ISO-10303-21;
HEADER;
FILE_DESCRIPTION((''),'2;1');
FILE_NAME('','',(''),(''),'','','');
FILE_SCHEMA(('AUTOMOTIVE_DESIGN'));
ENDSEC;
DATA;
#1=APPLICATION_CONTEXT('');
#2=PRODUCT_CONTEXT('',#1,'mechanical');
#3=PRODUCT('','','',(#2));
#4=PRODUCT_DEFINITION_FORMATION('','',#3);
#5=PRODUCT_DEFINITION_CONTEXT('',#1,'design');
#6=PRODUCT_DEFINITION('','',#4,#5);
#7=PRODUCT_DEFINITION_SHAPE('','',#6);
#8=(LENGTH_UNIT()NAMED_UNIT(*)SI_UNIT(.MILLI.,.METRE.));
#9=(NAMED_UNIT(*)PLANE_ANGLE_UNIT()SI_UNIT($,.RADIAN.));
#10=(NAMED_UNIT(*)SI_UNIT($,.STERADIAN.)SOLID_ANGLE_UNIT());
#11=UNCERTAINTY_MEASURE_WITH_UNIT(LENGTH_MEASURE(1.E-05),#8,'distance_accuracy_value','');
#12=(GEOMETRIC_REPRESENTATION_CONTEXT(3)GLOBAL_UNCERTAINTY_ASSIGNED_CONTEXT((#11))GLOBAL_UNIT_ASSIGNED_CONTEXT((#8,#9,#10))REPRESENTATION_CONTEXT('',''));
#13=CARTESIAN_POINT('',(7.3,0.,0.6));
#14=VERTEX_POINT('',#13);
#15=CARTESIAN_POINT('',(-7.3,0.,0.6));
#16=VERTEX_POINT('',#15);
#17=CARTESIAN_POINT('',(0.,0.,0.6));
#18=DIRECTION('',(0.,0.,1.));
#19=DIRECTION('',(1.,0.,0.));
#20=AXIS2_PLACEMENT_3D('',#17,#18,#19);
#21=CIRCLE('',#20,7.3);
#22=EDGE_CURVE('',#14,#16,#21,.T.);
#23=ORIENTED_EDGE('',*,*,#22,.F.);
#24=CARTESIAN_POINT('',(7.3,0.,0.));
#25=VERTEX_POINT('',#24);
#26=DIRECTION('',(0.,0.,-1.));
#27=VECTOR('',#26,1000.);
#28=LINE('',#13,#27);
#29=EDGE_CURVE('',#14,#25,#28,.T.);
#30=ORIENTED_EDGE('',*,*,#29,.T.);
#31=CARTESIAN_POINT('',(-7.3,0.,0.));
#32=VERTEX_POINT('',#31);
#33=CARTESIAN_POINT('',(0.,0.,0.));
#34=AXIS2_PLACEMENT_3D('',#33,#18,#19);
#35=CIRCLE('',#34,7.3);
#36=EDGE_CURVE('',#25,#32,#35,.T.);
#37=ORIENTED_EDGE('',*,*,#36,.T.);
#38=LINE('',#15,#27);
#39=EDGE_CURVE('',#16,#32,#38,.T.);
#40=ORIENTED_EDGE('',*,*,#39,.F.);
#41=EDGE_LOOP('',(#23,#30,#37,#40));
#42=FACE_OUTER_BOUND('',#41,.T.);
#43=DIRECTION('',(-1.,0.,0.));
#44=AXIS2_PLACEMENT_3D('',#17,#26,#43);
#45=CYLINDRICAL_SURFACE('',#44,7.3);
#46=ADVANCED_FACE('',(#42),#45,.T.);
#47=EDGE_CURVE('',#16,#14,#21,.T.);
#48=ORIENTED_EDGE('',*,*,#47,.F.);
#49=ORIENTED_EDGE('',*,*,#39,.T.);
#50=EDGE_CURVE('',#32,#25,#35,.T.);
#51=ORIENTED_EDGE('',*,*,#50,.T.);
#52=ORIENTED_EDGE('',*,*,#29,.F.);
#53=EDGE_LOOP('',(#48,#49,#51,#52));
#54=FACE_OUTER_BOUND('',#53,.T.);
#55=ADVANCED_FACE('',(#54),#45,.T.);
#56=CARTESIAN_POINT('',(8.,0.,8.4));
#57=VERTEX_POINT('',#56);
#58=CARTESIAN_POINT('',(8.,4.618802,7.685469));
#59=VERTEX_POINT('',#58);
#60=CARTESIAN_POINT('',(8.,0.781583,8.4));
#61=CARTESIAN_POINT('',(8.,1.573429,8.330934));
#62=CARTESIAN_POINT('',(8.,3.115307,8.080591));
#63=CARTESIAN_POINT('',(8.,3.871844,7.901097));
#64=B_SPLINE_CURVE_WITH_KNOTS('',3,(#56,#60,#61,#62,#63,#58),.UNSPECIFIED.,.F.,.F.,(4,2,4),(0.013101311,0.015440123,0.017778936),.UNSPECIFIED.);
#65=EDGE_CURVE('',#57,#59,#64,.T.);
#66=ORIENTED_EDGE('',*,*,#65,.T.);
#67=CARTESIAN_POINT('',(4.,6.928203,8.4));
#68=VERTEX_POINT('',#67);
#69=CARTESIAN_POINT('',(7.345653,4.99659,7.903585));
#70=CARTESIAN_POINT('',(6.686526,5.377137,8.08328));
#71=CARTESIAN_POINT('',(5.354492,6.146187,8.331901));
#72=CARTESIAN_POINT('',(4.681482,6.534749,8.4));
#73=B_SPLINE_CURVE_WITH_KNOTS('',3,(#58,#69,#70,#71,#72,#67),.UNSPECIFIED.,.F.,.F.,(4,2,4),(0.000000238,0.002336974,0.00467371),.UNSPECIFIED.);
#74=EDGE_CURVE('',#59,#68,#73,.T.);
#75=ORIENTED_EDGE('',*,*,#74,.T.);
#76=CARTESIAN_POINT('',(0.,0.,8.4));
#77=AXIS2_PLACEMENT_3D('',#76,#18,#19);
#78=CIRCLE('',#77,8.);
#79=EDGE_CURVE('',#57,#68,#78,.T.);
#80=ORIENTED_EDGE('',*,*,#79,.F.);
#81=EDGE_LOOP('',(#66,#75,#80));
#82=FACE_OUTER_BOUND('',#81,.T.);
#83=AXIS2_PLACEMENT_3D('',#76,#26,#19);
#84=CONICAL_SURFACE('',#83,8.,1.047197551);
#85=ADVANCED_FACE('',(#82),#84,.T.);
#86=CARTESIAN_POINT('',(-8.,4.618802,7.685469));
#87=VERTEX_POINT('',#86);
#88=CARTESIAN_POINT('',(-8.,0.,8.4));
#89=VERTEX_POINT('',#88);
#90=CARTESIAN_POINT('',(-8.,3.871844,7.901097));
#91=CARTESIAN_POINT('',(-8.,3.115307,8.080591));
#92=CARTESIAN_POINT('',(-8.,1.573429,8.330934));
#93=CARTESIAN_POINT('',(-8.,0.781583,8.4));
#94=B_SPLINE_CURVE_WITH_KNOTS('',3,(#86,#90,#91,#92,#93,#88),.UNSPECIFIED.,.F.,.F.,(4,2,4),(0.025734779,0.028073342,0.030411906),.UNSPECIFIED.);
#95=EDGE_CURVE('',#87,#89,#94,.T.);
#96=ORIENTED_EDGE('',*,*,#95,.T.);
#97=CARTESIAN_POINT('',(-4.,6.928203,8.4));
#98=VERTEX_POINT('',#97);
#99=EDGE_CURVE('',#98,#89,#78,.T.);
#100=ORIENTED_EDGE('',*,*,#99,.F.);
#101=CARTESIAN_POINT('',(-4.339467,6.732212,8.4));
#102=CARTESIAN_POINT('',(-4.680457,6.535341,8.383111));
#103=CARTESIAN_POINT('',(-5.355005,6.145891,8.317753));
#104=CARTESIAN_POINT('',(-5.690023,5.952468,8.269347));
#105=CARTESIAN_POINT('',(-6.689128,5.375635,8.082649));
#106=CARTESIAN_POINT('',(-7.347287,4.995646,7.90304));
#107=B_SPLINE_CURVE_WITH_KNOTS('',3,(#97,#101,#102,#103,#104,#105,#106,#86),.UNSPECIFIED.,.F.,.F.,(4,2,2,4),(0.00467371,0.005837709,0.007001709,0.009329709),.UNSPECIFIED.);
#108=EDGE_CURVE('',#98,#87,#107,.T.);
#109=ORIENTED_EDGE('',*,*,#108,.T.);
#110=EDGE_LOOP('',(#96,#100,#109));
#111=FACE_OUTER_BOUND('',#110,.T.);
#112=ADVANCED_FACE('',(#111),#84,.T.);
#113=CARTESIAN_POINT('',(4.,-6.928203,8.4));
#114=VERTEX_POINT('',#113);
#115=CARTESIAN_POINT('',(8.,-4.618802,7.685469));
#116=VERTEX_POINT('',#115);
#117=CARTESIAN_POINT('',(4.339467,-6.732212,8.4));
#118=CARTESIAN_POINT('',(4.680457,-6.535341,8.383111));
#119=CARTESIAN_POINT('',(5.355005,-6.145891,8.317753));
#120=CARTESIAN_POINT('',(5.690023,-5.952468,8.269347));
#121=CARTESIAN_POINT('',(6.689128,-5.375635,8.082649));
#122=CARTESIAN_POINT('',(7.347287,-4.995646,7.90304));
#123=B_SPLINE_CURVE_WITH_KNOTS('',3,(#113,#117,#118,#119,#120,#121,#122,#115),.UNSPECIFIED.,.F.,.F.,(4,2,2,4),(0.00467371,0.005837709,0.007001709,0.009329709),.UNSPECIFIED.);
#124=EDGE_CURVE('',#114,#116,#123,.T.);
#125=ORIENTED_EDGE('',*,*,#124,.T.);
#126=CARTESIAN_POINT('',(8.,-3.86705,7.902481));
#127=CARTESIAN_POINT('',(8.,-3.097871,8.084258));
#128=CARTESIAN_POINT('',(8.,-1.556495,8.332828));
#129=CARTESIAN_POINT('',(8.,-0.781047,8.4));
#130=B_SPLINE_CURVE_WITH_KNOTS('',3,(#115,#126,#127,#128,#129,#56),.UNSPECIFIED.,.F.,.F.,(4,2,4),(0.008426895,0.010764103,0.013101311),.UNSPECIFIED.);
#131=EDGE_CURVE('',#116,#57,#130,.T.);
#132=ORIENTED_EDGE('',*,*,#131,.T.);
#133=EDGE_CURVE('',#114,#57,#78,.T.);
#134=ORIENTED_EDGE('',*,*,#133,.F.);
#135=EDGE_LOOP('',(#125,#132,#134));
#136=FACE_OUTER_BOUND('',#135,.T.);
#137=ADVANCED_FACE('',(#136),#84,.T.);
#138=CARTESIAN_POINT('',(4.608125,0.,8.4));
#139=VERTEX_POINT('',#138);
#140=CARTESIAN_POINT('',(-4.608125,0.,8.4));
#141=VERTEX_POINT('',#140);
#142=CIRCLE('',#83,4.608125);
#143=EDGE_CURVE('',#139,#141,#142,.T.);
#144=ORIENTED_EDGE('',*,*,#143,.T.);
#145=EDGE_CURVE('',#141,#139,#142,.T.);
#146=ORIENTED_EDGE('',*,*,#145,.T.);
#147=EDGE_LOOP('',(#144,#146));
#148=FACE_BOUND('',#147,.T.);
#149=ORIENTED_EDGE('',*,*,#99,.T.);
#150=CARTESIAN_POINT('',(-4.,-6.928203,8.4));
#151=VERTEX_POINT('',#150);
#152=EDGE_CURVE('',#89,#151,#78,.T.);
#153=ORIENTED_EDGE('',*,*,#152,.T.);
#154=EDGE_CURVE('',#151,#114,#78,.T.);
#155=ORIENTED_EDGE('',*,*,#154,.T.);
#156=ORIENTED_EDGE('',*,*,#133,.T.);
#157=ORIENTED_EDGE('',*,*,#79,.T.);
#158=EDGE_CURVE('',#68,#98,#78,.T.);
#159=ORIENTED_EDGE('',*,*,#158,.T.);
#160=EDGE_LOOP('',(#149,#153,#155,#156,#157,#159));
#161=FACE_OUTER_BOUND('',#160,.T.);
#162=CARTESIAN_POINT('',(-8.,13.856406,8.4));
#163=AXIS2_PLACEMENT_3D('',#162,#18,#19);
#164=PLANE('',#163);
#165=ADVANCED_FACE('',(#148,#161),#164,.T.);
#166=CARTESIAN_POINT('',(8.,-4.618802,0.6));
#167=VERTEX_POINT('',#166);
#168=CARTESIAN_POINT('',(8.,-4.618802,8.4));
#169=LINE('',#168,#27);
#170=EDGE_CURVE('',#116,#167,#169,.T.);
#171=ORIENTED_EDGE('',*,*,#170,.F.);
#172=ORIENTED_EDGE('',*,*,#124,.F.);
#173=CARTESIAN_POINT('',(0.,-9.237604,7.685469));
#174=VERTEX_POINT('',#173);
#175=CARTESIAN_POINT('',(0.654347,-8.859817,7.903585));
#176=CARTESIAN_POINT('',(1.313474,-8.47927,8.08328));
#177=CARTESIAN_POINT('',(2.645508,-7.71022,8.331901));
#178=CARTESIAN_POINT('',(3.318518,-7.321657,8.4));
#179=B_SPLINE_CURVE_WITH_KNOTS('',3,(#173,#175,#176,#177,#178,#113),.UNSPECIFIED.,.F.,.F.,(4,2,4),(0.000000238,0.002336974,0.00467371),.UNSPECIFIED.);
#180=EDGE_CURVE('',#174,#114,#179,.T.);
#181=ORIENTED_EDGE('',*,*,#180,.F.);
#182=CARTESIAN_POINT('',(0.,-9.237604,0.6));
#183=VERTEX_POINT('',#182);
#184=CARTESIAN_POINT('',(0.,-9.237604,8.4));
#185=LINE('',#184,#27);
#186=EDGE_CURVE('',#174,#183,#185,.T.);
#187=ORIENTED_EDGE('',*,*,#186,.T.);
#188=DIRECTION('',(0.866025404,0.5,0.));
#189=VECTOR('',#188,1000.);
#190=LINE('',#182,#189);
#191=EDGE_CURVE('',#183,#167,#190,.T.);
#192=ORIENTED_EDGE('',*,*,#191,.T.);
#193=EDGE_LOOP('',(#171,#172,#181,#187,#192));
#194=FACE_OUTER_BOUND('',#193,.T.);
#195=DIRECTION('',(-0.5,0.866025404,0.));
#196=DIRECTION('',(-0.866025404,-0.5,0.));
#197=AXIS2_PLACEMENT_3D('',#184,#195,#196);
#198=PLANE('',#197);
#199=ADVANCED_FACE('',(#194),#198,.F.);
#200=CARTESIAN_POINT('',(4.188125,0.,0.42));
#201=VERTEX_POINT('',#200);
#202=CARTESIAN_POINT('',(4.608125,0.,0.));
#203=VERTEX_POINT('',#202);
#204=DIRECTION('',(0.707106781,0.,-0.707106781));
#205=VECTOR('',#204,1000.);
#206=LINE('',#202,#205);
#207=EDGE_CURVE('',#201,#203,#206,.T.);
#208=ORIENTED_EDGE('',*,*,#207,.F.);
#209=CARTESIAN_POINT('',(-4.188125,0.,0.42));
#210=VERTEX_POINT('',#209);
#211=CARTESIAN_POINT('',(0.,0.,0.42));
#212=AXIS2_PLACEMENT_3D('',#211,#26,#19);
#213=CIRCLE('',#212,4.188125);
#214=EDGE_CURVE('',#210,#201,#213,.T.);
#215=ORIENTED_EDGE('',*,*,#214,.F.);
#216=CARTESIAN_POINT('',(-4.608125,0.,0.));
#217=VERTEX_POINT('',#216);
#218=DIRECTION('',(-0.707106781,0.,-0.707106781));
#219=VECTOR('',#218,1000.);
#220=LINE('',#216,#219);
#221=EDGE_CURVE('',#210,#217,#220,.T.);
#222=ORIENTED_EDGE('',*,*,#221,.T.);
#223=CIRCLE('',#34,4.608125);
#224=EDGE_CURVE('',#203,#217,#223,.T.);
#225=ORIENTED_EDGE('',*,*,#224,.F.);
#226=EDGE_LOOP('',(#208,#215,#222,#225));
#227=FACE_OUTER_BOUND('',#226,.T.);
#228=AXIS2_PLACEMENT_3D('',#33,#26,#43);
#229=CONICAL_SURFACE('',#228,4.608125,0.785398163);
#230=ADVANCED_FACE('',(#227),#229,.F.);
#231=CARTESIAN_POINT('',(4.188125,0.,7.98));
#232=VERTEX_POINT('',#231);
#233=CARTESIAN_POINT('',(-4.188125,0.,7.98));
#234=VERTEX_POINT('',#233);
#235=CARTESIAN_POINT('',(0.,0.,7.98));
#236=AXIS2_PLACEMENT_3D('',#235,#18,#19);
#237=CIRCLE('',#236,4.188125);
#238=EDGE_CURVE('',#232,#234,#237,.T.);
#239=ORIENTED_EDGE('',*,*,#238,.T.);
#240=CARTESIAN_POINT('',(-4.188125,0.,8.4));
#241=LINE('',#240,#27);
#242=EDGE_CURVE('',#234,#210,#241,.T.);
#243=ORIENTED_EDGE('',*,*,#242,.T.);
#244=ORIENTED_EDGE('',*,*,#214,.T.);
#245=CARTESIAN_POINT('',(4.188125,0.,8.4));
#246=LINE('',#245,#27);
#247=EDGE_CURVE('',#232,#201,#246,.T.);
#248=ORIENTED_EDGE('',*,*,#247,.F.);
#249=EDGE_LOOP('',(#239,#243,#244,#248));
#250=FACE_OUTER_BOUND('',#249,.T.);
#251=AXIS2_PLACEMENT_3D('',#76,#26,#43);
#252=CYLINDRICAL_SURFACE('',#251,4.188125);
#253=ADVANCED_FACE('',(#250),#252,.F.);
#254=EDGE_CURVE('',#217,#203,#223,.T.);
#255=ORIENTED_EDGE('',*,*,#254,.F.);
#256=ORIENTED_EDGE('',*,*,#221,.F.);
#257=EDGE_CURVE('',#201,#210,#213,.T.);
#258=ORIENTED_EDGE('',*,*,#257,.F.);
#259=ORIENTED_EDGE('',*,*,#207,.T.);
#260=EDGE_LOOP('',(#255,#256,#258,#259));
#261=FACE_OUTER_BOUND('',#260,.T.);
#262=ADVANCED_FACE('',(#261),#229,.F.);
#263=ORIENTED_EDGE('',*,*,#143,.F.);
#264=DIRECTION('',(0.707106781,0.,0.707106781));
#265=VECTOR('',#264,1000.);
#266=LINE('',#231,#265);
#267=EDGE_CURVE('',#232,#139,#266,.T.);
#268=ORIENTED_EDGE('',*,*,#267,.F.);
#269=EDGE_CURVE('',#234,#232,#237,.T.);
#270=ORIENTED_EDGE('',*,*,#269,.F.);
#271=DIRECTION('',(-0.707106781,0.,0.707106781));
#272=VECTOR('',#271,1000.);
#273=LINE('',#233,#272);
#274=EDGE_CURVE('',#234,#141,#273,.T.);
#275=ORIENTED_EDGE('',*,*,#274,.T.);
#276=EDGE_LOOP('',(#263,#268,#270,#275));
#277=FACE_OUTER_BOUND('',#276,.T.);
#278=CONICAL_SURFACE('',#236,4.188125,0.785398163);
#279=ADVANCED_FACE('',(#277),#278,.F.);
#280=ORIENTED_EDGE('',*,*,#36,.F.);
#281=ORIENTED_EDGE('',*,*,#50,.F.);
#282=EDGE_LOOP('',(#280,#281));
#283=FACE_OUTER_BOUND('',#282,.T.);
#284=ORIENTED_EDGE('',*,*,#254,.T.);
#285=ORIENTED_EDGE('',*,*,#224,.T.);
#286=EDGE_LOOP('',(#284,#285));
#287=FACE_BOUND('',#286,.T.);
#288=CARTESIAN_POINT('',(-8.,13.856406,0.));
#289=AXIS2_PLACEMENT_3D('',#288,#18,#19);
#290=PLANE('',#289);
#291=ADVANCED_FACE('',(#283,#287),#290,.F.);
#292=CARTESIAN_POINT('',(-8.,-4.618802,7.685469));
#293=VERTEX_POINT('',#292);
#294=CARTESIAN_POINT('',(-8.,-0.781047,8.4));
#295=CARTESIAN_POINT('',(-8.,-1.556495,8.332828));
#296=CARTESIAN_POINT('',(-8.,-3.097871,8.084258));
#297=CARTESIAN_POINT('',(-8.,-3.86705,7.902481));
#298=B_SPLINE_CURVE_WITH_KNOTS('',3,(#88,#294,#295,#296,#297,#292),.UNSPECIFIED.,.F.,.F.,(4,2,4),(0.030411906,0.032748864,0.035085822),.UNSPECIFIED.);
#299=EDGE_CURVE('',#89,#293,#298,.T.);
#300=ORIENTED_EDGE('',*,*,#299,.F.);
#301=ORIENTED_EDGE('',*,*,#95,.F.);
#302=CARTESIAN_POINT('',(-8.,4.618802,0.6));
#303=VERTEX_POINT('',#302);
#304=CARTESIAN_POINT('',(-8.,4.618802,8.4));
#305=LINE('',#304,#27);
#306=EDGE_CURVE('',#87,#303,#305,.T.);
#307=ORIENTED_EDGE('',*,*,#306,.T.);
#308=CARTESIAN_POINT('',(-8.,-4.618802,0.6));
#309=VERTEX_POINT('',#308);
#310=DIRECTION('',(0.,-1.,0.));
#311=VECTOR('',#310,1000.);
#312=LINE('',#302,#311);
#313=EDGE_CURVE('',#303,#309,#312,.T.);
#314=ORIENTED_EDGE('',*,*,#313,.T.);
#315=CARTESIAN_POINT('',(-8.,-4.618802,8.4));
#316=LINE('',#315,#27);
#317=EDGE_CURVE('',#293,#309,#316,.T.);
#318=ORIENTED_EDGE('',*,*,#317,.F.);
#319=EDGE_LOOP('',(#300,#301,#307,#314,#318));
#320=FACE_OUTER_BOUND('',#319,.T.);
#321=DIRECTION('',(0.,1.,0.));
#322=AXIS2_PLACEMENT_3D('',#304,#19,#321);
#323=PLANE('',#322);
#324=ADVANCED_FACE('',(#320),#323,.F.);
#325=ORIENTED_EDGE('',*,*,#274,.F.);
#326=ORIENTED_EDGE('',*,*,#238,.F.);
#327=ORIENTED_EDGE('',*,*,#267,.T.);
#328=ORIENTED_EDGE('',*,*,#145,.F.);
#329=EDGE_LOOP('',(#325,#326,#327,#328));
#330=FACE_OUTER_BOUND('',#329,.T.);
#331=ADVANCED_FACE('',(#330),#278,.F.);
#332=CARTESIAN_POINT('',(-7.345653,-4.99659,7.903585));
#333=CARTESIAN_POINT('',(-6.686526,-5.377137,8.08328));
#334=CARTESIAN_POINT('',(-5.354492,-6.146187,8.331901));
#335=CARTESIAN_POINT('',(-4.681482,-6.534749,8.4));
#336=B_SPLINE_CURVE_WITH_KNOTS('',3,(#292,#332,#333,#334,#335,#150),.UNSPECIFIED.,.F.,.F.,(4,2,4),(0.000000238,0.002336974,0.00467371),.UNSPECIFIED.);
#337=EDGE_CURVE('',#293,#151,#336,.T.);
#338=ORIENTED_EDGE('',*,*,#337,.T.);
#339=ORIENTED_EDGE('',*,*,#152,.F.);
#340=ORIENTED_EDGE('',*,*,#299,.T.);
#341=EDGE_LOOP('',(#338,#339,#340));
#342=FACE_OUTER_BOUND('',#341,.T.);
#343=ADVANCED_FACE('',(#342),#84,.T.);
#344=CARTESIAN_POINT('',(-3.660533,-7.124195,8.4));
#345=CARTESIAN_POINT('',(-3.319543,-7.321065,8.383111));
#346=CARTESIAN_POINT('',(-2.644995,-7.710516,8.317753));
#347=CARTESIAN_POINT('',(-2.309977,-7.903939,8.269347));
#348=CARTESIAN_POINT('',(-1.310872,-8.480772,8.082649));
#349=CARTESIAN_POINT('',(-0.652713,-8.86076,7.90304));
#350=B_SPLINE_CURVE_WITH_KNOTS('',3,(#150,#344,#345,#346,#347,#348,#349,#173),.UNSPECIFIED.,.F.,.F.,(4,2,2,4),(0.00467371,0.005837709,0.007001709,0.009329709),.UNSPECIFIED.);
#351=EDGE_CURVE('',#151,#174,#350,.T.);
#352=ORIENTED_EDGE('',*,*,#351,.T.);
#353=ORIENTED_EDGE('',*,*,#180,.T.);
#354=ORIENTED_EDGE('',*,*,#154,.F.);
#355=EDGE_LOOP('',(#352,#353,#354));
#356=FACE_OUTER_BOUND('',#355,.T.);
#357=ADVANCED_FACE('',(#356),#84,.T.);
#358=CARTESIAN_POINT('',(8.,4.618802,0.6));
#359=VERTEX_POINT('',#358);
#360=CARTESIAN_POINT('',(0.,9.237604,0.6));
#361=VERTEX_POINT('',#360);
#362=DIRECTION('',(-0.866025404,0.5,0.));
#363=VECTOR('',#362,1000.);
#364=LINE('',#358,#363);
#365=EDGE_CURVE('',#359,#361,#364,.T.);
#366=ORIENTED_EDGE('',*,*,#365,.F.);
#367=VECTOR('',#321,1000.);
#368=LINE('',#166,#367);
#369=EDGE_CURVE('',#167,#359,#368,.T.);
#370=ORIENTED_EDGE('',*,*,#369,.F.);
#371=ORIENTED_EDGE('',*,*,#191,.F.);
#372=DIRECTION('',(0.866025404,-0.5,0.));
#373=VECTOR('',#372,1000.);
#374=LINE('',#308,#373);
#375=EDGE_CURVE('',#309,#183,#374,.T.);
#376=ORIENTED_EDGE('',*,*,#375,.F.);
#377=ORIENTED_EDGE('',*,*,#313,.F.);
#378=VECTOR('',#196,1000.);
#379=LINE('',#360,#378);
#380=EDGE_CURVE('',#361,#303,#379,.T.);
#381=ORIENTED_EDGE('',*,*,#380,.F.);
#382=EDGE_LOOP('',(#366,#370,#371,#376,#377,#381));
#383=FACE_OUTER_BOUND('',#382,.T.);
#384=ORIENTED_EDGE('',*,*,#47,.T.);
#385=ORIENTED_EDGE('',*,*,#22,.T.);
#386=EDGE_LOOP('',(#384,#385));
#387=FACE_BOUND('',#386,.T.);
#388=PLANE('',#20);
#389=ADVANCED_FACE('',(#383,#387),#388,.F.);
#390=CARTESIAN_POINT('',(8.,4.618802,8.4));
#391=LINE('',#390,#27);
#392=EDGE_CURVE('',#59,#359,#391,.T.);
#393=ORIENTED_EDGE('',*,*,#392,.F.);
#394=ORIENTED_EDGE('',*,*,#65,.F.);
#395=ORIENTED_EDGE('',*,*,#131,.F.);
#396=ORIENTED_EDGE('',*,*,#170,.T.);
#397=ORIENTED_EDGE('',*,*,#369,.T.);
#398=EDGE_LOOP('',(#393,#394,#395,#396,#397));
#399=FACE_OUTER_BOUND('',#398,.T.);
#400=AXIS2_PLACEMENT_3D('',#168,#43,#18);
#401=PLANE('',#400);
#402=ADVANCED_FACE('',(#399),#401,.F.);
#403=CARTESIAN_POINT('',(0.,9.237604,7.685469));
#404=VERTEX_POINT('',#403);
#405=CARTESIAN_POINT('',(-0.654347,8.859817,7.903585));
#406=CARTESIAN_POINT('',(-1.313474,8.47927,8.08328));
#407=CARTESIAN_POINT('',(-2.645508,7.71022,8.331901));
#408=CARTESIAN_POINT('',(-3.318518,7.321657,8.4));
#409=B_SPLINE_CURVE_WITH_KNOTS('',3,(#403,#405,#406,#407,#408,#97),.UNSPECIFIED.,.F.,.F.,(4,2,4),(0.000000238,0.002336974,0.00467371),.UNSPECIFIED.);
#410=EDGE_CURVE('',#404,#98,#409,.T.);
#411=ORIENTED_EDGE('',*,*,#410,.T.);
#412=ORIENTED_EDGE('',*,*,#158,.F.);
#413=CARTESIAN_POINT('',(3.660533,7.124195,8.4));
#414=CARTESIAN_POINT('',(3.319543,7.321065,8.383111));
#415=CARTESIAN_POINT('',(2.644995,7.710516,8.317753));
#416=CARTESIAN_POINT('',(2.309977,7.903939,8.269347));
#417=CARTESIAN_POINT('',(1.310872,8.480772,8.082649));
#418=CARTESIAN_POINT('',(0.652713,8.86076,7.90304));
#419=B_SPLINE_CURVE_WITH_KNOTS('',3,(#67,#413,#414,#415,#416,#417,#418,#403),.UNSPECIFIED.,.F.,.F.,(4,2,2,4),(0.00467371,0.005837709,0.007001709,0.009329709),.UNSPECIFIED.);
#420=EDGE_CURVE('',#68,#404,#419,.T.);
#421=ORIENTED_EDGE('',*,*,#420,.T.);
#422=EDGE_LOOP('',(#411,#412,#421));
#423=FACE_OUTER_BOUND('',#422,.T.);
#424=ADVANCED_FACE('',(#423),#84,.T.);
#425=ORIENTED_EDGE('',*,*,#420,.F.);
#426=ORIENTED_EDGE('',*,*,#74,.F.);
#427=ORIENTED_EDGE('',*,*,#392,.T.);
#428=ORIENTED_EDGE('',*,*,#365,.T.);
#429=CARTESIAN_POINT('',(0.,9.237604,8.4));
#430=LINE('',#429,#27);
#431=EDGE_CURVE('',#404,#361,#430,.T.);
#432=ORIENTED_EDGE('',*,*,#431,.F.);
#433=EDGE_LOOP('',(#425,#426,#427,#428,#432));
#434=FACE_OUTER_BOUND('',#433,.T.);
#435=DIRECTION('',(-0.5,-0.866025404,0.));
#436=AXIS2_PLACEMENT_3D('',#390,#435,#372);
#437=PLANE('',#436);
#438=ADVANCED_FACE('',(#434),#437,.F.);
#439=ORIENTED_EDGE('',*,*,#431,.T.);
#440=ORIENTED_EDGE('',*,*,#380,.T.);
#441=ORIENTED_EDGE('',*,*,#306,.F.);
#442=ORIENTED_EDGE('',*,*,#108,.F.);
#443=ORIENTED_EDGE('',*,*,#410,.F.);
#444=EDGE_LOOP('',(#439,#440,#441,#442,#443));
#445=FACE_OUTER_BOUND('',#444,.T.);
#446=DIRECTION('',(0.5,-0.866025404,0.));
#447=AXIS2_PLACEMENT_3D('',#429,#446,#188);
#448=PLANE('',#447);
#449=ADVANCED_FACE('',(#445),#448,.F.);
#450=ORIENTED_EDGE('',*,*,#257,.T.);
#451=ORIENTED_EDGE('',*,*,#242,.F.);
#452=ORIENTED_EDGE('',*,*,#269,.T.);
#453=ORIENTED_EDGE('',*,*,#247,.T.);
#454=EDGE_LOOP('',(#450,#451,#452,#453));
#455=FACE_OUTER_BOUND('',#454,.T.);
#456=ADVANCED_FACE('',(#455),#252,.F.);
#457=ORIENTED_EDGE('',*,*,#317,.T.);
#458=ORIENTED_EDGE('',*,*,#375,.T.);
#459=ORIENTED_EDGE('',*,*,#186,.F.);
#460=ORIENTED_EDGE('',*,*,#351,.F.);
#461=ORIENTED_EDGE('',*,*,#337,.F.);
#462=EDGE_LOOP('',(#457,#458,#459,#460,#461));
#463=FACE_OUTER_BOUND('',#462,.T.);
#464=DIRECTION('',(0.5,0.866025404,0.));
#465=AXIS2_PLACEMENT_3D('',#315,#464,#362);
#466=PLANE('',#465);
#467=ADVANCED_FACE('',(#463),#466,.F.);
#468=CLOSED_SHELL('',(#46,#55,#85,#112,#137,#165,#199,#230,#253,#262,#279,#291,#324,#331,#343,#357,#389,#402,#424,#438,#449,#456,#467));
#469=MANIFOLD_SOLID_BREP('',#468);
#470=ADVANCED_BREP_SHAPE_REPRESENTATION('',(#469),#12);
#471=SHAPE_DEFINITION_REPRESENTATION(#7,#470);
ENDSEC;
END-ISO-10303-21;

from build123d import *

# Parameters (mm, degrees)
SKETCH1_R          = 4.188125
EXTRUDE1_DEPTH     = 8.4
SKETCH2_OUTSIDE_W  = 23.168
SKETCH2_OUTSIDE_H  = 25.644
SKETCH2_OUTSIDE_R  = 7.3
CUT_EXTRUDE2_DEPTH = 0.6
SKETCH3_OUTSIDE_W  = 78.002
SKETCH3_OUTSIDE_H  = 80.478
SKETCH3_OUTSIDE_R  = 8
CUT_EXTRUDE3_DEPTH = 15.828800806
CUT_EXTRUDE3_DRAFT = -60
CHAMFER1_SIZE      = 0.42


with BuildPart() as part:
    # Sketch1 → Extrude1 (new body)
    with BuildSketch(Plane.XY):
        Polygon((0, 9.237604307), (-8, 4.618802154), (-8, -4.618802154), (0, -9.237604307), (8, -4.618802154), (8, 4.618802154), align=None)
        Circle(SKETCH1_R, mode=Mode.SUBTRACT)
    extrude(amount=EXTRUDE1_DEPTH)

    # Sketch2 outside → Cut-Extrude2 (cut)
    with BuildSketch(Plane.XY):
        Rectangle(SKETCH2_OUTSIDE_W, SKETCH2_OUTSIDE_H)
        Circle(SKETCH2_OUTSIDE_R, mode=Mode.SUBTRACT)
    extrude(amount=CUT_EXTRUDE2_DEPTH, mode=Mode.SUBTRACT)


with BuildPart() as cut_extrude3_tool:
    # Sketch3 outside → Cut-Extrude3 (with draft: the straight prism first)
    with BuildSketch(Plane.XY.offset(8.4)):
        Rectangle(SKETCH3_OUTSIDE_W, SKETCH3_OUTSIDE_H)
        Circle(SKETCH3_OUTSIDE_R, mode=Mode.SUBTRACT)
    extrude(amount=-CUT_EXTRUDE3_DEPTH)
    # Cut-Extrude3: the draft: its side faces are tilted about the plane it starts from
    cut_extrude3_sides = [cut_extrude3_tool.faces().sort_by_distance(p)[0] for p in [
        (0, -40.239, 0.485599597),
        (39.001, 0, 0.485599597),
        (0, 40.239, 0.485599597),
        (-39.001, 0, 0.485599597),
        (-8, 0, 0.485599597),
    ]]
    draft(cut_extrude3_sides, Plane.XY.offset(8.4), CUT_EXTRUDE3_DRAFT)


with BuildPart() as part_1:
    add(part.part)

    # Cut-Extrude3: cut by cut_extrude3_tool
    add(cut_extrude3_tool.part, mode=Mode.SUBTRACT)

    # Chamfer1
    chamfer1_edges = [part_1.edges().sort_by_distance(p)[0] for p in [
        (-4.188125, 0, 0),
        (-4.188125, 0, 8.4),
    ]]
    chamfer(chamfer1_edges, length=CHAMFER1_SIZE)


solid = part_1.part
